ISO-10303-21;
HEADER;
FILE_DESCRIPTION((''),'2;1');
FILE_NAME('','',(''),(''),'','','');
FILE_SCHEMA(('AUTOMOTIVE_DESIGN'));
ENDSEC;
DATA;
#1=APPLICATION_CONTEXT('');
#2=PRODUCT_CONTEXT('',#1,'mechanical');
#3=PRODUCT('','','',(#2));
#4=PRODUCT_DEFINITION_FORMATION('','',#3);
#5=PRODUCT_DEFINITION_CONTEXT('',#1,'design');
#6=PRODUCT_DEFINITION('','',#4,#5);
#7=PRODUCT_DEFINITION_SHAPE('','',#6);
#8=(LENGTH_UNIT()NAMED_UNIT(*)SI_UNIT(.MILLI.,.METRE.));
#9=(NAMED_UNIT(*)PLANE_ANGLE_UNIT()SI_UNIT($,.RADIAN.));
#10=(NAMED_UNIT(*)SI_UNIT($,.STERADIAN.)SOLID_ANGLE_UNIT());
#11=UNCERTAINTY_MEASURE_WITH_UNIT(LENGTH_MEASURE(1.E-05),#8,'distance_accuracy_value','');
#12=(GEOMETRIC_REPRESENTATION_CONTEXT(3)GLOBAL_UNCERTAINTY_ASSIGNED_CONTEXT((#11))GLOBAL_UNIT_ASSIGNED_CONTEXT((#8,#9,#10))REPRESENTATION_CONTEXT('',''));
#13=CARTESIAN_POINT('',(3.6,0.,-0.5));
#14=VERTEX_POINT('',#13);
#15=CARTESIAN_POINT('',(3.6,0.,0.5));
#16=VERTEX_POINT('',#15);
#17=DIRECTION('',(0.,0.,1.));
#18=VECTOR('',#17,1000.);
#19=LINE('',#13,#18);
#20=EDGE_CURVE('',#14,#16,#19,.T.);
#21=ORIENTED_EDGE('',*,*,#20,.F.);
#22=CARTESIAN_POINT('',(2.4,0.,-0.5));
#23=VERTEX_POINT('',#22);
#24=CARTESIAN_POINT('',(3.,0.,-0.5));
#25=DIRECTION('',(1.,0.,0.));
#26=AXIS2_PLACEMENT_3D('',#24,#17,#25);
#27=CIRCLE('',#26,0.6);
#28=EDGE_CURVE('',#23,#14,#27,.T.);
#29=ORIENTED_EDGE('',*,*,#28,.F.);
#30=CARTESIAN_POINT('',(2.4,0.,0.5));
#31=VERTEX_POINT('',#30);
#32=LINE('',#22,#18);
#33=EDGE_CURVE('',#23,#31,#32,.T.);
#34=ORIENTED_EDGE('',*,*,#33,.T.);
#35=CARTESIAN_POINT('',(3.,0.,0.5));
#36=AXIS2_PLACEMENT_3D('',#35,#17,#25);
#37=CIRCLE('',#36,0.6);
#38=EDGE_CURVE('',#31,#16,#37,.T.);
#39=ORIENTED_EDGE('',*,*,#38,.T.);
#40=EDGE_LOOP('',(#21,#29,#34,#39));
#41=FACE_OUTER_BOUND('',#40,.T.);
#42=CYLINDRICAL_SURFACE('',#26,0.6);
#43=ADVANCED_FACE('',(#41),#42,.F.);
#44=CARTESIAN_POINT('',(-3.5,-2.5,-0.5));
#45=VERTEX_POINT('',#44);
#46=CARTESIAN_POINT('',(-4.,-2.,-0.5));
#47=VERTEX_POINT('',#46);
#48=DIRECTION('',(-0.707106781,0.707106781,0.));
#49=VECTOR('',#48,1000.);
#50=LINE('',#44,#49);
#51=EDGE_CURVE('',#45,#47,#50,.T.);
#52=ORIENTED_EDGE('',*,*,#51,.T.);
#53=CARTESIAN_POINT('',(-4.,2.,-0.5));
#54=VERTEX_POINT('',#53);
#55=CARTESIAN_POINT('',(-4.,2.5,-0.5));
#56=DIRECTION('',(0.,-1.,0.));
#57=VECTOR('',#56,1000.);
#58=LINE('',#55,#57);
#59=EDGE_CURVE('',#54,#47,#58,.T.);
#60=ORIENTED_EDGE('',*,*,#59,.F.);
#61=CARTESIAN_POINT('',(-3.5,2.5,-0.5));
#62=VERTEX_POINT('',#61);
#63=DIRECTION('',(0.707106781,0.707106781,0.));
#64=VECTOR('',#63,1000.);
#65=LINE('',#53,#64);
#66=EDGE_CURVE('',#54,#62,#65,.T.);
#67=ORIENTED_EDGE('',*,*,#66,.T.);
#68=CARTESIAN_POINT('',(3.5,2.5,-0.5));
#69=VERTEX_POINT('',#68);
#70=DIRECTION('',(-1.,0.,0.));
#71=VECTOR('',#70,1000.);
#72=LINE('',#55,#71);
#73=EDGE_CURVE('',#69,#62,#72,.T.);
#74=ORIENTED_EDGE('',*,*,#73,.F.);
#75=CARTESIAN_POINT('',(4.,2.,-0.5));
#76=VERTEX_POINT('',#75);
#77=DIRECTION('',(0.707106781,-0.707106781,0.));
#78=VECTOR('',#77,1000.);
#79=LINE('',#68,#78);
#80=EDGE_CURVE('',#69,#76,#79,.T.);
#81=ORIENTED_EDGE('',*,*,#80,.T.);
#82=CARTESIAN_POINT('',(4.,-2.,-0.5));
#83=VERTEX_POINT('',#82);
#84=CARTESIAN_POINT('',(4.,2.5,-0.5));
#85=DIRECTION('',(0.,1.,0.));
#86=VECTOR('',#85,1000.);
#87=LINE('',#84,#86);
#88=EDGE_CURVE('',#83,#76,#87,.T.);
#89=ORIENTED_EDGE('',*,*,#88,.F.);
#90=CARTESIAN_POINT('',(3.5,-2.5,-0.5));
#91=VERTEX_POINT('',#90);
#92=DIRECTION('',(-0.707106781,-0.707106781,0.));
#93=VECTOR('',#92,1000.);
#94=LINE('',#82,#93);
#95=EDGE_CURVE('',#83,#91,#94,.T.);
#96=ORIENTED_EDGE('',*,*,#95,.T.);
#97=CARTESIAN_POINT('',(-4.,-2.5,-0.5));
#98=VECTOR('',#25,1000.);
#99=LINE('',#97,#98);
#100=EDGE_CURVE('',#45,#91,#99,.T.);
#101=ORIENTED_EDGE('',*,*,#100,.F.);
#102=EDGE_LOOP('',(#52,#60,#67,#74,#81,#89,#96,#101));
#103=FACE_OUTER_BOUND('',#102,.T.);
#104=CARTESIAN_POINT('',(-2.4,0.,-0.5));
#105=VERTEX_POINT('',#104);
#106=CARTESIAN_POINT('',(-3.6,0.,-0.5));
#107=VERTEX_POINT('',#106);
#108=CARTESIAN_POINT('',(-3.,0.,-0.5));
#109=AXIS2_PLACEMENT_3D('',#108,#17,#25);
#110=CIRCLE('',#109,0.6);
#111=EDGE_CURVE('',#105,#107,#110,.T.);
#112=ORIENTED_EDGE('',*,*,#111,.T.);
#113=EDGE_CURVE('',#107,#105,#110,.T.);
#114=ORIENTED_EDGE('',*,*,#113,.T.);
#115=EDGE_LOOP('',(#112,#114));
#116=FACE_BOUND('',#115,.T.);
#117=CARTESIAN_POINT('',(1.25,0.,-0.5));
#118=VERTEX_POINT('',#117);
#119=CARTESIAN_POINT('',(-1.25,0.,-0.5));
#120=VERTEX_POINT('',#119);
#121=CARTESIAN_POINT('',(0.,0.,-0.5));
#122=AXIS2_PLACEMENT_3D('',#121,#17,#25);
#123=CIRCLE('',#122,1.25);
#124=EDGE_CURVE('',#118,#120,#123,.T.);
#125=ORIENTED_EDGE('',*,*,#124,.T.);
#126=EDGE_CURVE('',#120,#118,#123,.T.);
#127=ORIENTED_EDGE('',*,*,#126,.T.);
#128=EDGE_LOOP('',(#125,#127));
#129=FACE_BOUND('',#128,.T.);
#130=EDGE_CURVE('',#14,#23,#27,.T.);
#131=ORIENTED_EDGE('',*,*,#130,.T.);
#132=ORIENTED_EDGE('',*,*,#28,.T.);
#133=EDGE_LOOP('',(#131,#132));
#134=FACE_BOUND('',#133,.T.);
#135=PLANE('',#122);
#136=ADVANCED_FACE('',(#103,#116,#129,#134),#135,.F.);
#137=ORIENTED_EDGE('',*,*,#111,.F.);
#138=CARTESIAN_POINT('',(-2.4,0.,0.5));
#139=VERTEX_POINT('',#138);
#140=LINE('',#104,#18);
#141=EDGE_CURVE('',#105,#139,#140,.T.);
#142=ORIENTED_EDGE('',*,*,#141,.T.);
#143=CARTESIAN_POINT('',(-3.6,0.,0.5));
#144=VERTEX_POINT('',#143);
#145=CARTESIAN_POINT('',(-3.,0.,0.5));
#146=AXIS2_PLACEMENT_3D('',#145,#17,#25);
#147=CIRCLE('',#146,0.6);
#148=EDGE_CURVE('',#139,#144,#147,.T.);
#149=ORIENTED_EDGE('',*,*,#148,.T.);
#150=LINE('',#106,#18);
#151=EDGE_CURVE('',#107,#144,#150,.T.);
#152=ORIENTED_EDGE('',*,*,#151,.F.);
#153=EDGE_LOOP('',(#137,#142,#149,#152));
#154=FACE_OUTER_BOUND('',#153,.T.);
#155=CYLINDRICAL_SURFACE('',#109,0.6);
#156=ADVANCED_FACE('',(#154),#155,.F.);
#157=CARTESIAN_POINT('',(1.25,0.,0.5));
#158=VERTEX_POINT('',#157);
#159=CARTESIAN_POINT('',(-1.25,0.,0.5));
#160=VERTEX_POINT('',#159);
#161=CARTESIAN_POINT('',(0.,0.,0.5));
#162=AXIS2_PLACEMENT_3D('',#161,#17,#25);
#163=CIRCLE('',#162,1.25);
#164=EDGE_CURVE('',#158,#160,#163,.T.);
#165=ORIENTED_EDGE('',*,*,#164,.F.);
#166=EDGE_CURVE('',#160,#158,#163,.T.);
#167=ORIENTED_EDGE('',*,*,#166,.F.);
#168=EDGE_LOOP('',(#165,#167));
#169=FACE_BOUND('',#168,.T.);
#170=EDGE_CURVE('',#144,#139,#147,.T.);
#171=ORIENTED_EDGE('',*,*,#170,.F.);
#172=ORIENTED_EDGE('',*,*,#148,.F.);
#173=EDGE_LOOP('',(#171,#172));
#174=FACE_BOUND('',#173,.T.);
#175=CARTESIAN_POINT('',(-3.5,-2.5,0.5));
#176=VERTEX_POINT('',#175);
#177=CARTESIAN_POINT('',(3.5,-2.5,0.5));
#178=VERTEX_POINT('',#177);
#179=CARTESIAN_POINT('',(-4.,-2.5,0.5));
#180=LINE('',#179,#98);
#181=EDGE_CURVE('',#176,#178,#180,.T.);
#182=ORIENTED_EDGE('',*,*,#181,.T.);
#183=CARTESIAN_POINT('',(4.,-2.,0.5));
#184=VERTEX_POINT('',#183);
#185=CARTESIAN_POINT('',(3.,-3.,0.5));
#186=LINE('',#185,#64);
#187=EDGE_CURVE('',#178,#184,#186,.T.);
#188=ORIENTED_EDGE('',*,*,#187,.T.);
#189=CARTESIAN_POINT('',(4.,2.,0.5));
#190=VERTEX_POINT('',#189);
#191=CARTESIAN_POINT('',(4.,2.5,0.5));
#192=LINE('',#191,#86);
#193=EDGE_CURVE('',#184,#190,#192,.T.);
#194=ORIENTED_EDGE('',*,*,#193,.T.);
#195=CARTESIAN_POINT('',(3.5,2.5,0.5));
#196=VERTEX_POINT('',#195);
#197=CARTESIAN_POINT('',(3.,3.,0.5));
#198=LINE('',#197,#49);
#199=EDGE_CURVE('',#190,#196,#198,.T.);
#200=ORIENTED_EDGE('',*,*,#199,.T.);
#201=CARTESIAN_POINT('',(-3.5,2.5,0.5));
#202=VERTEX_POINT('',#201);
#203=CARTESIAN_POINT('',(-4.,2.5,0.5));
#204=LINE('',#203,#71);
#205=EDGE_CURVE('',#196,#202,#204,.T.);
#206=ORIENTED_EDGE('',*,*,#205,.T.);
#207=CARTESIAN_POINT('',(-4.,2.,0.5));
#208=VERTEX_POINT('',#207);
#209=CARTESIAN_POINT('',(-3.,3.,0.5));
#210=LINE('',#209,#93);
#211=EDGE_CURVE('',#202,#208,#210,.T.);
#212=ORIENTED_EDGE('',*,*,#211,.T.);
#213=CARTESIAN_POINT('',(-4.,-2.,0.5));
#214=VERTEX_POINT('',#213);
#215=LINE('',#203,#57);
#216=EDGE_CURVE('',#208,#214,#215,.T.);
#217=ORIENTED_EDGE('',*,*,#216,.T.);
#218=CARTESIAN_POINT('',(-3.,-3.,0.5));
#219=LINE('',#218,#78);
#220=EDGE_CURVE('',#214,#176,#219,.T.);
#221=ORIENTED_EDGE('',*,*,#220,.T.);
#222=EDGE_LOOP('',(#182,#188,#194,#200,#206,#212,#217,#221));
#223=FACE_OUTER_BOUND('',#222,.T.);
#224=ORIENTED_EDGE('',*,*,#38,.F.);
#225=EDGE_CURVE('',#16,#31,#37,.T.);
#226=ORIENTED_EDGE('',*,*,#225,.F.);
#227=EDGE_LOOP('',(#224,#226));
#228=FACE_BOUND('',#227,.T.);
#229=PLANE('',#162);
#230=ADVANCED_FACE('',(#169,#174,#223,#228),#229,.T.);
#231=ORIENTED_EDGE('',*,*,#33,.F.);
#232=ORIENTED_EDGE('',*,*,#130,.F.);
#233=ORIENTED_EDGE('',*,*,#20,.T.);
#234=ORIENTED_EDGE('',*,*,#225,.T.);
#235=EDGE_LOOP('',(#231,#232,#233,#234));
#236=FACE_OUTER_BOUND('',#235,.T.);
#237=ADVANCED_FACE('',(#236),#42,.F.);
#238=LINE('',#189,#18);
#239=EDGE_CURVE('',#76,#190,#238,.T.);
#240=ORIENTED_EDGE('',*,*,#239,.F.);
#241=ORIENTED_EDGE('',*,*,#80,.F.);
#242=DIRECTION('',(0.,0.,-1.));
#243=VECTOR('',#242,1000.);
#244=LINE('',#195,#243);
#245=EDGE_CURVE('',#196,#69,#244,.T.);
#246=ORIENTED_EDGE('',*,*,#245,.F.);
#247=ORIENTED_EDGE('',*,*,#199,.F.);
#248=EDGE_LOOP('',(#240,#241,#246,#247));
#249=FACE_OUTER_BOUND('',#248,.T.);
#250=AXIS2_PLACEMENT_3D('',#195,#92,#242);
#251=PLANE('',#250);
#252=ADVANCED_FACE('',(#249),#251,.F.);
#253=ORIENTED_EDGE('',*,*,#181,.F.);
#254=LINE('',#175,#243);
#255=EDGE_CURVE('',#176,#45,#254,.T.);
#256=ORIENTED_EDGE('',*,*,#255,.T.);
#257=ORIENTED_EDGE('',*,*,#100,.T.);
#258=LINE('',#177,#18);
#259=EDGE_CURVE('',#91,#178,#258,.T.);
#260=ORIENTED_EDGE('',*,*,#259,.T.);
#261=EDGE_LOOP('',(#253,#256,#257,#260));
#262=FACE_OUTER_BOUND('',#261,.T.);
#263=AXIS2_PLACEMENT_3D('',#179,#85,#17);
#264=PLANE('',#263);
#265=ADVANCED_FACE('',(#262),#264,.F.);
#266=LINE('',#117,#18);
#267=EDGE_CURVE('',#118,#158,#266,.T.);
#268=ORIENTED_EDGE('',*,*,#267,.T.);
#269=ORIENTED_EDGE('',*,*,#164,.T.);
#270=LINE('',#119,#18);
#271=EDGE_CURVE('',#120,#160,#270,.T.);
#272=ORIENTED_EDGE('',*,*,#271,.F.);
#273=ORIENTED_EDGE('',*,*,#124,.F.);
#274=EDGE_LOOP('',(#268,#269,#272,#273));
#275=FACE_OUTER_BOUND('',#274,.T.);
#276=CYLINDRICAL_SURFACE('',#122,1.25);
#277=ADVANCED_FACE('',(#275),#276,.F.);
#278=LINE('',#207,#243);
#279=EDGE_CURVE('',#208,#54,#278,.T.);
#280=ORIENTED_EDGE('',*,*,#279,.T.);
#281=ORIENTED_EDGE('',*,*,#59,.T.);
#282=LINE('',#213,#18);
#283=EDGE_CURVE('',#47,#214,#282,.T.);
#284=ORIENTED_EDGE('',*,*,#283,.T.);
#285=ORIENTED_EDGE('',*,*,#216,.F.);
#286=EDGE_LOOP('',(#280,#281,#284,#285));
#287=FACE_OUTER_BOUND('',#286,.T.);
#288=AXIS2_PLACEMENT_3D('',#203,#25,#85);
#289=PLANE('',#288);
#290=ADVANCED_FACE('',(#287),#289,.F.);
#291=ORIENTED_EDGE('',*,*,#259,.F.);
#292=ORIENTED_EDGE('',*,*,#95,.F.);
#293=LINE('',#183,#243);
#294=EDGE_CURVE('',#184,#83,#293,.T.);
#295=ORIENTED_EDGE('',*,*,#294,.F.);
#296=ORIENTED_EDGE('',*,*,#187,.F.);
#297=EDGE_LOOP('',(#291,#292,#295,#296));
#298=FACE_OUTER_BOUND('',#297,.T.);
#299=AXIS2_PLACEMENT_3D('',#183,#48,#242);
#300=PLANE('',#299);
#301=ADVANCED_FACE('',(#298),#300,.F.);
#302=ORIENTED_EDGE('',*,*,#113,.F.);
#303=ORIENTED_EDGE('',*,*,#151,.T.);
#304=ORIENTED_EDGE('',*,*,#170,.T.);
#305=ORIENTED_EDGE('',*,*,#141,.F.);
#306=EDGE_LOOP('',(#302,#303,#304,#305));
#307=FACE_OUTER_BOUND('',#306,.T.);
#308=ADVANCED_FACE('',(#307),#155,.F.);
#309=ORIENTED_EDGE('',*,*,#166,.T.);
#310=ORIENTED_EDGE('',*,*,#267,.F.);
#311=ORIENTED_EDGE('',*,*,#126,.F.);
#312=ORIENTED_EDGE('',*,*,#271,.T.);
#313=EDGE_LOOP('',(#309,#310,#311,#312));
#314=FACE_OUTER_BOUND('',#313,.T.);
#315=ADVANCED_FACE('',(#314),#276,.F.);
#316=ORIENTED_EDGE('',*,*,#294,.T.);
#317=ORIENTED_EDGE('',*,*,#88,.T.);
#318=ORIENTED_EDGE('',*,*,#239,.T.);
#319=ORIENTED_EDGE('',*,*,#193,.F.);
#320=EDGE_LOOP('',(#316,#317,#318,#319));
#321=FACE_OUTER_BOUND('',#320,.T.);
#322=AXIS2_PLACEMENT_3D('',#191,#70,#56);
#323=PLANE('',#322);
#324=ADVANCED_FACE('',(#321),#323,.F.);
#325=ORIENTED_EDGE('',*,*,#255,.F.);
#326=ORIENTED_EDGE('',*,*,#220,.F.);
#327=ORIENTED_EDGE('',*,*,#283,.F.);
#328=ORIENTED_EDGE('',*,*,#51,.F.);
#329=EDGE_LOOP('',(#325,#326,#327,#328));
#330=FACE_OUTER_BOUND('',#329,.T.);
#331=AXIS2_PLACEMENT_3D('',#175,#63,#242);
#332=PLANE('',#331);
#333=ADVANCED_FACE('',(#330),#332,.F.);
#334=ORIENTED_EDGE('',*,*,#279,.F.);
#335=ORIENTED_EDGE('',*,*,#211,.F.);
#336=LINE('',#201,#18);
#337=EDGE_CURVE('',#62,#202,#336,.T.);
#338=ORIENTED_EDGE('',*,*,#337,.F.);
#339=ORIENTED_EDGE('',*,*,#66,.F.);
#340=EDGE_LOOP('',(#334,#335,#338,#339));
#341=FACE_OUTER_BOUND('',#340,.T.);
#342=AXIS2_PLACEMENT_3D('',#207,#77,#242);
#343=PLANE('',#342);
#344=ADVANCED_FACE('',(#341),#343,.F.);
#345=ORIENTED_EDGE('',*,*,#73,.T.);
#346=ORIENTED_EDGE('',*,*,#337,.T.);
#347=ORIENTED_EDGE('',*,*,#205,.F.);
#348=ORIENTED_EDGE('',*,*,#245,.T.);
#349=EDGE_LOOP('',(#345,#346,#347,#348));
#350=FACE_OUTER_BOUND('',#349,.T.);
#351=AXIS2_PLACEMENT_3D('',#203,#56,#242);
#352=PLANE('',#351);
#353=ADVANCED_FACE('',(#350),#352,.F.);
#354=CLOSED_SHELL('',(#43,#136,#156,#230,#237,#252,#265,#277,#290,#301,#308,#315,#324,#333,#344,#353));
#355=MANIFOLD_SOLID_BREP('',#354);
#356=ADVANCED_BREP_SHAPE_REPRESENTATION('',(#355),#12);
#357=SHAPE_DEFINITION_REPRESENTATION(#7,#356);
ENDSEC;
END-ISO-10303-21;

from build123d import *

# Parameters (mm, degrees)
SKETCH1_W           = 8
SKETCH1_H           = 5
BOSS_EXTRUDE1_DEPTH = 0.5
SKETCH2_R           = 1.25
SKETCH2_R_2         = 0.6
CUT_EXTRUDE1_DEPTH  = 5.82182538
CHAMFER1_SIZE       = 0.5


with BuildPart() as part:
    # Sketch1 → Boss-Extrude1 (new, symmetric)
    with BuildSketch(Plane.XY):
        Rectangle(SKETCH1_W, SKETCH1_H)
    extrude(amount=BOSS_EXTRUDE1_DEPTH, both=True)

    # Sketch2 → Cut-Extrude1 (cut, through all)
    with BuildSketch(Plane.XY.offset(0.5)):
        Circle(SKETCH2_R)
        with Locations((-3, 0)):
            Circle(SKETCH2_R_2)
        with Locations((3, 0)):
            Circle(SKETCH2_R_2)
    extrude(amount=-CUT_EXTRUDE1_DEPTH, mode=Mode.SUBTRACT)

    # Chamfer1
    chamfer1_edges = [part.edges().sort_by_distance(p)[0] for p in [
        (4, -2.5, 0),
        (-4, -2.5, 0),
        (-4, 2.5, 0),
        (4, 2.5, 0),
    ]]
    chamfer(chamfer1_edges, length=CHAMFER1_SIZE)


solid = part.part
